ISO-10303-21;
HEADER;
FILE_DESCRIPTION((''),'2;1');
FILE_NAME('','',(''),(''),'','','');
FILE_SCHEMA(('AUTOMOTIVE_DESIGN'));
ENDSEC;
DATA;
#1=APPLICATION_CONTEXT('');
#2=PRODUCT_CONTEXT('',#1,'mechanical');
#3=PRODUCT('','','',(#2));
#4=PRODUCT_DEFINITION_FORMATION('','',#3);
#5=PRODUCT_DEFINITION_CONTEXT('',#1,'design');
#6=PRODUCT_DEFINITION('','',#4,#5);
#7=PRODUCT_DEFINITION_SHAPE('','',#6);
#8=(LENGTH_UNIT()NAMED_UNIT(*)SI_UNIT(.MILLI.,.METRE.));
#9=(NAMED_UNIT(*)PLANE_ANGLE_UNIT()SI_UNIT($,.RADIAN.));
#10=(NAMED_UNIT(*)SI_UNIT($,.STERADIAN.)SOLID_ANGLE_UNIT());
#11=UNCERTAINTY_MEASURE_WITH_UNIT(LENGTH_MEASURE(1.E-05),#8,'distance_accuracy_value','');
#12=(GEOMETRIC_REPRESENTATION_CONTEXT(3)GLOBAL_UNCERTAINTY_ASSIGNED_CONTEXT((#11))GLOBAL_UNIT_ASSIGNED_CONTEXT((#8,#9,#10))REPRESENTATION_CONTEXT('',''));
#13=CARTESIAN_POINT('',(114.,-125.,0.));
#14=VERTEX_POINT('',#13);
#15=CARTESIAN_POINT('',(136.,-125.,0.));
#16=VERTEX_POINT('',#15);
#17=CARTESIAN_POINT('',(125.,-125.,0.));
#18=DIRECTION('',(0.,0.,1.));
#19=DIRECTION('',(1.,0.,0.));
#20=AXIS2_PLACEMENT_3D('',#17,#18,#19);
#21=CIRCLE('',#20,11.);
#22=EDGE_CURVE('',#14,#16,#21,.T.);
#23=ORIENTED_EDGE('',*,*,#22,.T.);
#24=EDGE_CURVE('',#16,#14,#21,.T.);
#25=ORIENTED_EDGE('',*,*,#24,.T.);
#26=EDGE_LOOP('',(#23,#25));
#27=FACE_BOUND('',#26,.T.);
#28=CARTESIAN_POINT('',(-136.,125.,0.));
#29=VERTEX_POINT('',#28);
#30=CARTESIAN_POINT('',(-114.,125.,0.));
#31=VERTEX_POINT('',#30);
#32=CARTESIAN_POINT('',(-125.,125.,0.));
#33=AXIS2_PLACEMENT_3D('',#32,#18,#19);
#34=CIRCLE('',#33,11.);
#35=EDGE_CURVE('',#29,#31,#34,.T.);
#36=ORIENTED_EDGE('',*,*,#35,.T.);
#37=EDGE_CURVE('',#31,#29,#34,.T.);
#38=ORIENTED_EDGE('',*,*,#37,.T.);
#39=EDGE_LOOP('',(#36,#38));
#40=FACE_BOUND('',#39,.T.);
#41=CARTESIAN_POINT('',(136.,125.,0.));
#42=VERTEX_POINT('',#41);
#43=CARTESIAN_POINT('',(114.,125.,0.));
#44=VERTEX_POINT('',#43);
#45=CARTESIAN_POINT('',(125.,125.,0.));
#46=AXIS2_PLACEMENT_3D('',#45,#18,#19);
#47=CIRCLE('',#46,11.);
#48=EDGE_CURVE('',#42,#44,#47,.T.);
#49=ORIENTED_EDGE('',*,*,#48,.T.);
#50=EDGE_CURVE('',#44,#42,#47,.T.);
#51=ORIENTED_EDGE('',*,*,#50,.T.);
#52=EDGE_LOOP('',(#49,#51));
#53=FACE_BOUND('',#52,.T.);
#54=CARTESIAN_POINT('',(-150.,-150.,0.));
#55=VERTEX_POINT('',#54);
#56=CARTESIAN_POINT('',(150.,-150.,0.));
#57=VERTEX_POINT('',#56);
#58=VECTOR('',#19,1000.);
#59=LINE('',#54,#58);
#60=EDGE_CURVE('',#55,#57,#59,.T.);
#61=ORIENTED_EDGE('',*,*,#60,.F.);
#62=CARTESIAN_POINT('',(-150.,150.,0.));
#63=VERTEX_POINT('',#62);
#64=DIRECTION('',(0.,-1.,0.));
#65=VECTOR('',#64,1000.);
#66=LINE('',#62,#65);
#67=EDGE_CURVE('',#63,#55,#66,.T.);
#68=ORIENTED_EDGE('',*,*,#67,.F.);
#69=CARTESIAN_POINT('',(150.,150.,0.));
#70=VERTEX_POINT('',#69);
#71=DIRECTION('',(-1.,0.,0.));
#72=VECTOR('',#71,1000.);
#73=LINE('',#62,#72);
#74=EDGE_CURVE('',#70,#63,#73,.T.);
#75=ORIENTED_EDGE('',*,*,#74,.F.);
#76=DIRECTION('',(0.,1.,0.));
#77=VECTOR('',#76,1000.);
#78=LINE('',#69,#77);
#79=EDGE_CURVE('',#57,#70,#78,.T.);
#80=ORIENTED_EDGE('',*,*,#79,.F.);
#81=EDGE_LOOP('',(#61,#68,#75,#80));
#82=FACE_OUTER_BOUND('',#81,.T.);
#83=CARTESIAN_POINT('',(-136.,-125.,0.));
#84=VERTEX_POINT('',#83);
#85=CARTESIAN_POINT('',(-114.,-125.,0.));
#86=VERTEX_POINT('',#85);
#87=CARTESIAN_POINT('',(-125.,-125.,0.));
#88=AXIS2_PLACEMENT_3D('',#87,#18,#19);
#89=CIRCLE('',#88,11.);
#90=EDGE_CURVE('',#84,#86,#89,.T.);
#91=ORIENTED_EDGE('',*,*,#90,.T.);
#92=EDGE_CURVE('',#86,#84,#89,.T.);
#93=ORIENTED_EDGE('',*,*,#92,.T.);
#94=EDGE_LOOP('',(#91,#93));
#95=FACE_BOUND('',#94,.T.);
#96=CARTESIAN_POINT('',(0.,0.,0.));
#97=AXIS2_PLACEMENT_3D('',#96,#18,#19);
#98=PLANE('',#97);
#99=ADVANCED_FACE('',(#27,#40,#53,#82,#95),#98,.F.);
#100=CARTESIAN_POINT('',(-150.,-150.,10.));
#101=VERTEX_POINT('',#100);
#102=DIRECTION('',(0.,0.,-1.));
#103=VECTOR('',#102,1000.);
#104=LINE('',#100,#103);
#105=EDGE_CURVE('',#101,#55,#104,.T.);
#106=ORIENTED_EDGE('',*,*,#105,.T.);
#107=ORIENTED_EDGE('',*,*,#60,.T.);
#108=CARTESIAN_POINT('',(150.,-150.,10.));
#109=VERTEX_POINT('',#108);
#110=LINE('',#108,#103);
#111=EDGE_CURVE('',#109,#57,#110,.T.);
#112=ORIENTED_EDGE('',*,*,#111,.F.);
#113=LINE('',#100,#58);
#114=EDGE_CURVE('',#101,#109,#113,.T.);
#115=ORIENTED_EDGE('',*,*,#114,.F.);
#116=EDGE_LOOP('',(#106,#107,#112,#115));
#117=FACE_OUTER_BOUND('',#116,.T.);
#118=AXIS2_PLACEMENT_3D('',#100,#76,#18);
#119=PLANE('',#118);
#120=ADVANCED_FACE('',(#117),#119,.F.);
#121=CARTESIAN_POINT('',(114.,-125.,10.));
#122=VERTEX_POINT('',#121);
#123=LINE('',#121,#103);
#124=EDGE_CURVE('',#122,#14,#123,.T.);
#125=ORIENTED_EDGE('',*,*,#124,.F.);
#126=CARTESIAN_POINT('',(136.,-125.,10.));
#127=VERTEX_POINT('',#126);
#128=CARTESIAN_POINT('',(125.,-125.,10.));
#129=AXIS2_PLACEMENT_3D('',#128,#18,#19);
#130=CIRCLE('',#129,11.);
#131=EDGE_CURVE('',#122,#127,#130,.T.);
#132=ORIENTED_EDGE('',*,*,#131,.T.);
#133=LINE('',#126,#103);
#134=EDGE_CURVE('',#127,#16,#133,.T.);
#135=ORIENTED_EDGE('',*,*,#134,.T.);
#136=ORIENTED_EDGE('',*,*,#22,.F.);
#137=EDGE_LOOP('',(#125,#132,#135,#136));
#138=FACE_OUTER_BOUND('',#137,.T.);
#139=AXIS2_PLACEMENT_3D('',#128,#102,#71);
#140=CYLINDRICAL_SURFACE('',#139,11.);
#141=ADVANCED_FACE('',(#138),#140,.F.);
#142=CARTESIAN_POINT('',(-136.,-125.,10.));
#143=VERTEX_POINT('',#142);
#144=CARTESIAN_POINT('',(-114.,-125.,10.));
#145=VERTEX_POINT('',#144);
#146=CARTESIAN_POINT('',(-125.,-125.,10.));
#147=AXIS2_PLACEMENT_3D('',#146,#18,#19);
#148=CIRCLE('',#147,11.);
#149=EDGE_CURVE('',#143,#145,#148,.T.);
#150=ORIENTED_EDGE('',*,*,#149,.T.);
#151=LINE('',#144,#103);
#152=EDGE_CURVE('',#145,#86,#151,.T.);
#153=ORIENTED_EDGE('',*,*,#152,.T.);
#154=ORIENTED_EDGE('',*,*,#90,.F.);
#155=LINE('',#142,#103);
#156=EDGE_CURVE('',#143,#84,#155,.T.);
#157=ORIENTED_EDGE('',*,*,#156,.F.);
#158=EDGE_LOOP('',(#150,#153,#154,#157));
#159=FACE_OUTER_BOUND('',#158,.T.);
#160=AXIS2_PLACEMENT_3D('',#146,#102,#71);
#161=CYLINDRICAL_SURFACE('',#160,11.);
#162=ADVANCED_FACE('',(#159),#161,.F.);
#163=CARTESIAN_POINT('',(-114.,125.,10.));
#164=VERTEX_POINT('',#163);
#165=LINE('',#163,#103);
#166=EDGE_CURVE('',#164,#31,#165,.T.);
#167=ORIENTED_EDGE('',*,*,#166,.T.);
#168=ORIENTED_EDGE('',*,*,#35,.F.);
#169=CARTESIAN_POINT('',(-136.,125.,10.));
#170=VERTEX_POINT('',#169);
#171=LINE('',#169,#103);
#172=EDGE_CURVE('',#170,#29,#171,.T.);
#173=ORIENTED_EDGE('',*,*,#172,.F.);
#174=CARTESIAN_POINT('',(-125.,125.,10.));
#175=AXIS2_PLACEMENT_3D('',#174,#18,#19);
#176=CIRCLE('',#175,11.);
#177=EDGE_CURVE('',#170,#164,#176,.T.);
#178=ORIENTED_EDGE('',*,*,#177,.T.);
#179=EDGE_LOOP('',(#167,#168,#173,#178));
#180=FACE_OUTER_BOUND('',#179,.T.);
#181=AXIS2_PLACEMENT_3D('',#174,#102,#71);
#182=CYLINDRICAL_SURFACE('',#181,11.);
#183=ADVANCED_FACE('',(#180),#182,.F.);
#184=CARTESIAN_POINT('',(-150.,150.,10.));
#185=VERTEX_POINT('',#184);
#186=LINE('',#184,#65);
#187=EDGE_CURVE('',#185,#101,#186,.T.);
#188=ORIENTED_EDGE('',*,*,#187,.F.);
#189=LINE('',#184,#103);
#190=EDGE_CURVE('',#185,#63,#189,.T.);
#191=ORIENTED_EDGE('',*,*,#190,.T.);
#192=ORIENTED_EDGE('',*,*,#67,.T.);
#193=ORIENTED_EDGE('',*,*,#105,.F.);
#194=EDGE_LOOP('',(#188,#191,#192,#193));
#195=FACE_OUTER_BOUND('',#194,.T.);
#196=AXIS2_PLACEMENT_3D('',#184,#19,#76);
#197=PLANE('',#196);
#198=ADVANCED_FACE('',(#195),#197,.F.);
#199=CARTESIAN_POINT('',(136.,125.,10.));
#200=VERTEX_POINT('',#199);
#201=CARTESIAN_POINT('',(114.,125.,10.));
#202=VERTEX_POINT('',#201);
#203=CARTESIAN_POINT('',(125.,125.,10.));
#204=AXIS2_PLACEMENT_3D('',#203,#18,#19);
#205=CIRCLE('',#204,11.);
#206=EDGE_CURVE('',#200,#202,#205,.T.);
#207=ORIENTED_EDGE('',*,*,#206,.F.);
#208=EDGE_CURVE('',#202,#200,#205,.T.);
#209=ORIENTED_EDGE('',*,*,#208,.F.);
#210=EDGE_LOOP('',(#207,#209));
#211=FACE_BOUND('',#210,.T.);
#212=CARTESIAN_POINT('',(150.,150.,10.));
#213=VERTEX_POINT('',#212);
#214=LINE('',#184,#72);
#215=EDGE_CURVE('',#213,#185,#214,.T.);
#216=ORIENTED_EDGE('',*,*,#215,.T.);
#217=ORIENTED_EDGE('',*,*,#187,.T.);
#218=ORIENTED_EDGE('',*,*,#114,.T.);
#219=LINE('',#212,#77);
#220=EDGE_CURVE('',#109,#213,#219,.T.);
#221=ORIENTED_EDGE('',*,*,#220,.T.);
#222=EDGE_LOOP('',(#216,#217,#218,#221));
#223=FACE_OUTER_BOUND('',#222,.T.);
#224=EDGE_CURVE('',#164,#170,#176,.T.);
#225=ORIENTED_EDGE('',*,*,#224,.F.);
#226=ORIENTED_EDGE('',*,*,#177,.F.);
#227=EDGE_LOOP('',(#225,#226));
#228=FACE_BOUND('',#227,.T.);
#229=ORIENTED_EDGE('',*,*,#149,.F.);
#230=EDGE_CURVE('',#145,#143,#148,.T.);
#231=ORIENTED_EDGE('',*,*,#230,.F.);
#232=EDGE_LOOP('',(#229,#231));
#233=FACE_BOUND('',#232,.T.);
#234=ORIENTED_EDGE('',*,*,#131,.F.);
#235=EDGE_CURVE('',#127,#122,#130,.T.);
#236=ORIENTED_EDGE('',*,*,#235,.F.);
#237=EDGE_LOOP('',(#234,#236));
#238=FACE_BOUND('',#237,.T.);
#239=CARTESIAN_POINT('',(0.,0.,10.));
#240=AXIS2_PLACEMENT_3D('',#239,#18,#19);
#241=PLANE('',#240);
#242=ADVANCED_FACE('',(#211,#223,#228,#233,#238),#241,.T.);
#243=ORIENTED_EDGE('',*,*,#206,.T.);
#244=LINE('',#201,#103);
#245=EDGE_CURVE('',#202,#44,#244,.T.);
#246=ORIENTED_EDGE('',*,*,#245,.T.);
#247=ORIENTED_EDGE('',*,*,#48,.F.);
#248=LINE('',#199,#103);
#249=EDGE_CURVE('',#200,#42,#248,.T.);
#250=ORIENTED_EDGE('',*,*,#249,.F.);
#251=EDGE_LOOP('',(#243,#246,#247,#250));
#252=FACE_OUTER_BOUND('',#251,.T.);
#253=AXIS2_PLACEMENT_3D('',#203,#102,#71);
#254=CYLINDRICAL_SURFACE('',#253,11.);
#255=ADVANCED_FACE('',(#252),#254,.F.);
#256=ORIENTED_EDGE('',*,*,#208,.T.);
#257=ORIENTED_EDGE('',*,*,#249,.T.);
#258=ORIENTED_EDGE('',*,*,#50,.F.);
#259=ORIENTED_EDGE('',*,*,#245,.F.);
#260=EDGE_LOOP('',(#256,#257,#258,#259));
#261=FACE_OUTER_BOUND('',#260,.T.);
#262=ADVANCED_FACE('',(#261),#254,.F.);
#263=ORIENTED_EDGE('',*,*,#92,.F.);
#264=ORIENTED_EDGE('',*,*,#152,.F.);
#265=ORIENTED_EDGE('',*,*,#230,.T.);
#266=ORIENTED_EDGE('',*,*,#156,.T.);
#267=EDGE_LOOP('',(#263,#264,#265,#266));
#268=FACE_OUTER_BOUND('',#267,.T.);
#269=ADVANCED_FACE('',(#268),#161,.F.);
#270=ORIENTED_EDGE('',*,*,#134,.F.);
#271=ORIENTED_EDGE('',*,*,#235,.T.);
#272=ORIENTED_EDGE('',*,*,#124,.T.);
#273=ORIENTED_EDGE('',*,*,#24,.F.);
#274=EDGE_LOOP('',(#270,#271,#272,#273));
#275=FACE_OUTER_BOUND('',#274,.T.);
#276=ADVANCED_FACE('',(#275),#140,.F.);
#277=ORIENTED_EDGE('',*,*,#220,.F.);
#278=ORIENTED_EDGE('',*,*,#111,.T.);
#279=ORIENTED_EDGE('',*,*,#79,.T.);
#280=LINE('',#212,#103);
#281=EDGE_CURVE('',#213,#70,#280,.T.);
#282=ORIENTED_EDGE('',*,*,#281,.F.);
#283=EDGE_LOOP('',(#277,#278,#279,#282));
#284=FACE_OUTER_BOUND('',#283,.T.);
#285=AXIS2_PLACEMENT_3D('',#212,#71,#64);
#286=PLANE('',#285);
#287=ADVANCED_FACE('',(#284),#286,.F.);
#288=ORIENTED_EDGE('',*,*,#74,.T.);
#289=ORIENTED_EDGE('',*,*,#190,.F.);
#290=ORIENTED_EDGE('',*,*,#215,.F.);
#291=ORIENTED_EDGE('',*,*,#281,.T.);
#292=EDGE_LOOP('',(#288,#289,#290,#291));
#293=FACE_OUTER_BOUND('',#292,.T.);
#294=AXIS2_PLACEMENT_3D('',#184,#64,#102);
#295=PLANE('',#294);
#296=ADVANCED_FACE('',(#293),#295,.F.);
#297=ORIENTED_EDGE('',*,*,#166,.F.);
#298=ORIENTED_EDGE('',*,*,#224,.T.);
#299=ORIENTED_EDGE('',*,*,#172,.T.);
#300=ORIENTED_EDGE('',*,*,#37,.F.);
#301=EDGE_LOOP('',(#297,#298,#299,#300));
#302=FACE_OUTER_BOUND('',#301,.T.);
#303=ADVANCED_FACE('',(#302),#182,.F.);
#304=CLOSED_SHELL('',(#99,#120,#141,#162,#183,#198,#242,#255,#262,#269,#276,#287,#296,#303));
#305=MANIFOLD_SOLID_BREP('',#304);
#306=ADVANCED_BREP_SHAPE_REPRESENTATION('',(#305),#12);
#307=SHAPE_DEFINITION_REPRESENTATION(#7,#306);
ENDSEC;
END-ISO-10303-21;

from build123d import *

# Parameters (mm, degrees)
SKETCH1_W           = 300
SKETCH1_H           = 300
SKETCH1_R           = 11
BOSS_EXTRUDE1_DEPTH = 10


with BuildPart() as part:
    # Sketch1 → Boss-Extrude1 (new body)
    with BuildSketch(Plane.XY):
        Rectangle(SKETCH1_W, SKETCH1_H)
        with Locations((-125, 125)):
            Circle(SKETCH1_R, mode=Mode.SUBTRACT)
        with Locations((125, 125)):
            Circle(SKETCH1_R, mode=Mode.SUBTRACT)
        with Locations((125, -125)):
            Circle(SKETCH1_R, mode=Mode.SUBTRACT)
        with Locations((-125, -125)):
            Circle(SKETCH1_R, mode=Mode.SUBTRACT)
    extrude(amount=BOSS_EXTRUDE1_DEPTH)


solid = part.part
